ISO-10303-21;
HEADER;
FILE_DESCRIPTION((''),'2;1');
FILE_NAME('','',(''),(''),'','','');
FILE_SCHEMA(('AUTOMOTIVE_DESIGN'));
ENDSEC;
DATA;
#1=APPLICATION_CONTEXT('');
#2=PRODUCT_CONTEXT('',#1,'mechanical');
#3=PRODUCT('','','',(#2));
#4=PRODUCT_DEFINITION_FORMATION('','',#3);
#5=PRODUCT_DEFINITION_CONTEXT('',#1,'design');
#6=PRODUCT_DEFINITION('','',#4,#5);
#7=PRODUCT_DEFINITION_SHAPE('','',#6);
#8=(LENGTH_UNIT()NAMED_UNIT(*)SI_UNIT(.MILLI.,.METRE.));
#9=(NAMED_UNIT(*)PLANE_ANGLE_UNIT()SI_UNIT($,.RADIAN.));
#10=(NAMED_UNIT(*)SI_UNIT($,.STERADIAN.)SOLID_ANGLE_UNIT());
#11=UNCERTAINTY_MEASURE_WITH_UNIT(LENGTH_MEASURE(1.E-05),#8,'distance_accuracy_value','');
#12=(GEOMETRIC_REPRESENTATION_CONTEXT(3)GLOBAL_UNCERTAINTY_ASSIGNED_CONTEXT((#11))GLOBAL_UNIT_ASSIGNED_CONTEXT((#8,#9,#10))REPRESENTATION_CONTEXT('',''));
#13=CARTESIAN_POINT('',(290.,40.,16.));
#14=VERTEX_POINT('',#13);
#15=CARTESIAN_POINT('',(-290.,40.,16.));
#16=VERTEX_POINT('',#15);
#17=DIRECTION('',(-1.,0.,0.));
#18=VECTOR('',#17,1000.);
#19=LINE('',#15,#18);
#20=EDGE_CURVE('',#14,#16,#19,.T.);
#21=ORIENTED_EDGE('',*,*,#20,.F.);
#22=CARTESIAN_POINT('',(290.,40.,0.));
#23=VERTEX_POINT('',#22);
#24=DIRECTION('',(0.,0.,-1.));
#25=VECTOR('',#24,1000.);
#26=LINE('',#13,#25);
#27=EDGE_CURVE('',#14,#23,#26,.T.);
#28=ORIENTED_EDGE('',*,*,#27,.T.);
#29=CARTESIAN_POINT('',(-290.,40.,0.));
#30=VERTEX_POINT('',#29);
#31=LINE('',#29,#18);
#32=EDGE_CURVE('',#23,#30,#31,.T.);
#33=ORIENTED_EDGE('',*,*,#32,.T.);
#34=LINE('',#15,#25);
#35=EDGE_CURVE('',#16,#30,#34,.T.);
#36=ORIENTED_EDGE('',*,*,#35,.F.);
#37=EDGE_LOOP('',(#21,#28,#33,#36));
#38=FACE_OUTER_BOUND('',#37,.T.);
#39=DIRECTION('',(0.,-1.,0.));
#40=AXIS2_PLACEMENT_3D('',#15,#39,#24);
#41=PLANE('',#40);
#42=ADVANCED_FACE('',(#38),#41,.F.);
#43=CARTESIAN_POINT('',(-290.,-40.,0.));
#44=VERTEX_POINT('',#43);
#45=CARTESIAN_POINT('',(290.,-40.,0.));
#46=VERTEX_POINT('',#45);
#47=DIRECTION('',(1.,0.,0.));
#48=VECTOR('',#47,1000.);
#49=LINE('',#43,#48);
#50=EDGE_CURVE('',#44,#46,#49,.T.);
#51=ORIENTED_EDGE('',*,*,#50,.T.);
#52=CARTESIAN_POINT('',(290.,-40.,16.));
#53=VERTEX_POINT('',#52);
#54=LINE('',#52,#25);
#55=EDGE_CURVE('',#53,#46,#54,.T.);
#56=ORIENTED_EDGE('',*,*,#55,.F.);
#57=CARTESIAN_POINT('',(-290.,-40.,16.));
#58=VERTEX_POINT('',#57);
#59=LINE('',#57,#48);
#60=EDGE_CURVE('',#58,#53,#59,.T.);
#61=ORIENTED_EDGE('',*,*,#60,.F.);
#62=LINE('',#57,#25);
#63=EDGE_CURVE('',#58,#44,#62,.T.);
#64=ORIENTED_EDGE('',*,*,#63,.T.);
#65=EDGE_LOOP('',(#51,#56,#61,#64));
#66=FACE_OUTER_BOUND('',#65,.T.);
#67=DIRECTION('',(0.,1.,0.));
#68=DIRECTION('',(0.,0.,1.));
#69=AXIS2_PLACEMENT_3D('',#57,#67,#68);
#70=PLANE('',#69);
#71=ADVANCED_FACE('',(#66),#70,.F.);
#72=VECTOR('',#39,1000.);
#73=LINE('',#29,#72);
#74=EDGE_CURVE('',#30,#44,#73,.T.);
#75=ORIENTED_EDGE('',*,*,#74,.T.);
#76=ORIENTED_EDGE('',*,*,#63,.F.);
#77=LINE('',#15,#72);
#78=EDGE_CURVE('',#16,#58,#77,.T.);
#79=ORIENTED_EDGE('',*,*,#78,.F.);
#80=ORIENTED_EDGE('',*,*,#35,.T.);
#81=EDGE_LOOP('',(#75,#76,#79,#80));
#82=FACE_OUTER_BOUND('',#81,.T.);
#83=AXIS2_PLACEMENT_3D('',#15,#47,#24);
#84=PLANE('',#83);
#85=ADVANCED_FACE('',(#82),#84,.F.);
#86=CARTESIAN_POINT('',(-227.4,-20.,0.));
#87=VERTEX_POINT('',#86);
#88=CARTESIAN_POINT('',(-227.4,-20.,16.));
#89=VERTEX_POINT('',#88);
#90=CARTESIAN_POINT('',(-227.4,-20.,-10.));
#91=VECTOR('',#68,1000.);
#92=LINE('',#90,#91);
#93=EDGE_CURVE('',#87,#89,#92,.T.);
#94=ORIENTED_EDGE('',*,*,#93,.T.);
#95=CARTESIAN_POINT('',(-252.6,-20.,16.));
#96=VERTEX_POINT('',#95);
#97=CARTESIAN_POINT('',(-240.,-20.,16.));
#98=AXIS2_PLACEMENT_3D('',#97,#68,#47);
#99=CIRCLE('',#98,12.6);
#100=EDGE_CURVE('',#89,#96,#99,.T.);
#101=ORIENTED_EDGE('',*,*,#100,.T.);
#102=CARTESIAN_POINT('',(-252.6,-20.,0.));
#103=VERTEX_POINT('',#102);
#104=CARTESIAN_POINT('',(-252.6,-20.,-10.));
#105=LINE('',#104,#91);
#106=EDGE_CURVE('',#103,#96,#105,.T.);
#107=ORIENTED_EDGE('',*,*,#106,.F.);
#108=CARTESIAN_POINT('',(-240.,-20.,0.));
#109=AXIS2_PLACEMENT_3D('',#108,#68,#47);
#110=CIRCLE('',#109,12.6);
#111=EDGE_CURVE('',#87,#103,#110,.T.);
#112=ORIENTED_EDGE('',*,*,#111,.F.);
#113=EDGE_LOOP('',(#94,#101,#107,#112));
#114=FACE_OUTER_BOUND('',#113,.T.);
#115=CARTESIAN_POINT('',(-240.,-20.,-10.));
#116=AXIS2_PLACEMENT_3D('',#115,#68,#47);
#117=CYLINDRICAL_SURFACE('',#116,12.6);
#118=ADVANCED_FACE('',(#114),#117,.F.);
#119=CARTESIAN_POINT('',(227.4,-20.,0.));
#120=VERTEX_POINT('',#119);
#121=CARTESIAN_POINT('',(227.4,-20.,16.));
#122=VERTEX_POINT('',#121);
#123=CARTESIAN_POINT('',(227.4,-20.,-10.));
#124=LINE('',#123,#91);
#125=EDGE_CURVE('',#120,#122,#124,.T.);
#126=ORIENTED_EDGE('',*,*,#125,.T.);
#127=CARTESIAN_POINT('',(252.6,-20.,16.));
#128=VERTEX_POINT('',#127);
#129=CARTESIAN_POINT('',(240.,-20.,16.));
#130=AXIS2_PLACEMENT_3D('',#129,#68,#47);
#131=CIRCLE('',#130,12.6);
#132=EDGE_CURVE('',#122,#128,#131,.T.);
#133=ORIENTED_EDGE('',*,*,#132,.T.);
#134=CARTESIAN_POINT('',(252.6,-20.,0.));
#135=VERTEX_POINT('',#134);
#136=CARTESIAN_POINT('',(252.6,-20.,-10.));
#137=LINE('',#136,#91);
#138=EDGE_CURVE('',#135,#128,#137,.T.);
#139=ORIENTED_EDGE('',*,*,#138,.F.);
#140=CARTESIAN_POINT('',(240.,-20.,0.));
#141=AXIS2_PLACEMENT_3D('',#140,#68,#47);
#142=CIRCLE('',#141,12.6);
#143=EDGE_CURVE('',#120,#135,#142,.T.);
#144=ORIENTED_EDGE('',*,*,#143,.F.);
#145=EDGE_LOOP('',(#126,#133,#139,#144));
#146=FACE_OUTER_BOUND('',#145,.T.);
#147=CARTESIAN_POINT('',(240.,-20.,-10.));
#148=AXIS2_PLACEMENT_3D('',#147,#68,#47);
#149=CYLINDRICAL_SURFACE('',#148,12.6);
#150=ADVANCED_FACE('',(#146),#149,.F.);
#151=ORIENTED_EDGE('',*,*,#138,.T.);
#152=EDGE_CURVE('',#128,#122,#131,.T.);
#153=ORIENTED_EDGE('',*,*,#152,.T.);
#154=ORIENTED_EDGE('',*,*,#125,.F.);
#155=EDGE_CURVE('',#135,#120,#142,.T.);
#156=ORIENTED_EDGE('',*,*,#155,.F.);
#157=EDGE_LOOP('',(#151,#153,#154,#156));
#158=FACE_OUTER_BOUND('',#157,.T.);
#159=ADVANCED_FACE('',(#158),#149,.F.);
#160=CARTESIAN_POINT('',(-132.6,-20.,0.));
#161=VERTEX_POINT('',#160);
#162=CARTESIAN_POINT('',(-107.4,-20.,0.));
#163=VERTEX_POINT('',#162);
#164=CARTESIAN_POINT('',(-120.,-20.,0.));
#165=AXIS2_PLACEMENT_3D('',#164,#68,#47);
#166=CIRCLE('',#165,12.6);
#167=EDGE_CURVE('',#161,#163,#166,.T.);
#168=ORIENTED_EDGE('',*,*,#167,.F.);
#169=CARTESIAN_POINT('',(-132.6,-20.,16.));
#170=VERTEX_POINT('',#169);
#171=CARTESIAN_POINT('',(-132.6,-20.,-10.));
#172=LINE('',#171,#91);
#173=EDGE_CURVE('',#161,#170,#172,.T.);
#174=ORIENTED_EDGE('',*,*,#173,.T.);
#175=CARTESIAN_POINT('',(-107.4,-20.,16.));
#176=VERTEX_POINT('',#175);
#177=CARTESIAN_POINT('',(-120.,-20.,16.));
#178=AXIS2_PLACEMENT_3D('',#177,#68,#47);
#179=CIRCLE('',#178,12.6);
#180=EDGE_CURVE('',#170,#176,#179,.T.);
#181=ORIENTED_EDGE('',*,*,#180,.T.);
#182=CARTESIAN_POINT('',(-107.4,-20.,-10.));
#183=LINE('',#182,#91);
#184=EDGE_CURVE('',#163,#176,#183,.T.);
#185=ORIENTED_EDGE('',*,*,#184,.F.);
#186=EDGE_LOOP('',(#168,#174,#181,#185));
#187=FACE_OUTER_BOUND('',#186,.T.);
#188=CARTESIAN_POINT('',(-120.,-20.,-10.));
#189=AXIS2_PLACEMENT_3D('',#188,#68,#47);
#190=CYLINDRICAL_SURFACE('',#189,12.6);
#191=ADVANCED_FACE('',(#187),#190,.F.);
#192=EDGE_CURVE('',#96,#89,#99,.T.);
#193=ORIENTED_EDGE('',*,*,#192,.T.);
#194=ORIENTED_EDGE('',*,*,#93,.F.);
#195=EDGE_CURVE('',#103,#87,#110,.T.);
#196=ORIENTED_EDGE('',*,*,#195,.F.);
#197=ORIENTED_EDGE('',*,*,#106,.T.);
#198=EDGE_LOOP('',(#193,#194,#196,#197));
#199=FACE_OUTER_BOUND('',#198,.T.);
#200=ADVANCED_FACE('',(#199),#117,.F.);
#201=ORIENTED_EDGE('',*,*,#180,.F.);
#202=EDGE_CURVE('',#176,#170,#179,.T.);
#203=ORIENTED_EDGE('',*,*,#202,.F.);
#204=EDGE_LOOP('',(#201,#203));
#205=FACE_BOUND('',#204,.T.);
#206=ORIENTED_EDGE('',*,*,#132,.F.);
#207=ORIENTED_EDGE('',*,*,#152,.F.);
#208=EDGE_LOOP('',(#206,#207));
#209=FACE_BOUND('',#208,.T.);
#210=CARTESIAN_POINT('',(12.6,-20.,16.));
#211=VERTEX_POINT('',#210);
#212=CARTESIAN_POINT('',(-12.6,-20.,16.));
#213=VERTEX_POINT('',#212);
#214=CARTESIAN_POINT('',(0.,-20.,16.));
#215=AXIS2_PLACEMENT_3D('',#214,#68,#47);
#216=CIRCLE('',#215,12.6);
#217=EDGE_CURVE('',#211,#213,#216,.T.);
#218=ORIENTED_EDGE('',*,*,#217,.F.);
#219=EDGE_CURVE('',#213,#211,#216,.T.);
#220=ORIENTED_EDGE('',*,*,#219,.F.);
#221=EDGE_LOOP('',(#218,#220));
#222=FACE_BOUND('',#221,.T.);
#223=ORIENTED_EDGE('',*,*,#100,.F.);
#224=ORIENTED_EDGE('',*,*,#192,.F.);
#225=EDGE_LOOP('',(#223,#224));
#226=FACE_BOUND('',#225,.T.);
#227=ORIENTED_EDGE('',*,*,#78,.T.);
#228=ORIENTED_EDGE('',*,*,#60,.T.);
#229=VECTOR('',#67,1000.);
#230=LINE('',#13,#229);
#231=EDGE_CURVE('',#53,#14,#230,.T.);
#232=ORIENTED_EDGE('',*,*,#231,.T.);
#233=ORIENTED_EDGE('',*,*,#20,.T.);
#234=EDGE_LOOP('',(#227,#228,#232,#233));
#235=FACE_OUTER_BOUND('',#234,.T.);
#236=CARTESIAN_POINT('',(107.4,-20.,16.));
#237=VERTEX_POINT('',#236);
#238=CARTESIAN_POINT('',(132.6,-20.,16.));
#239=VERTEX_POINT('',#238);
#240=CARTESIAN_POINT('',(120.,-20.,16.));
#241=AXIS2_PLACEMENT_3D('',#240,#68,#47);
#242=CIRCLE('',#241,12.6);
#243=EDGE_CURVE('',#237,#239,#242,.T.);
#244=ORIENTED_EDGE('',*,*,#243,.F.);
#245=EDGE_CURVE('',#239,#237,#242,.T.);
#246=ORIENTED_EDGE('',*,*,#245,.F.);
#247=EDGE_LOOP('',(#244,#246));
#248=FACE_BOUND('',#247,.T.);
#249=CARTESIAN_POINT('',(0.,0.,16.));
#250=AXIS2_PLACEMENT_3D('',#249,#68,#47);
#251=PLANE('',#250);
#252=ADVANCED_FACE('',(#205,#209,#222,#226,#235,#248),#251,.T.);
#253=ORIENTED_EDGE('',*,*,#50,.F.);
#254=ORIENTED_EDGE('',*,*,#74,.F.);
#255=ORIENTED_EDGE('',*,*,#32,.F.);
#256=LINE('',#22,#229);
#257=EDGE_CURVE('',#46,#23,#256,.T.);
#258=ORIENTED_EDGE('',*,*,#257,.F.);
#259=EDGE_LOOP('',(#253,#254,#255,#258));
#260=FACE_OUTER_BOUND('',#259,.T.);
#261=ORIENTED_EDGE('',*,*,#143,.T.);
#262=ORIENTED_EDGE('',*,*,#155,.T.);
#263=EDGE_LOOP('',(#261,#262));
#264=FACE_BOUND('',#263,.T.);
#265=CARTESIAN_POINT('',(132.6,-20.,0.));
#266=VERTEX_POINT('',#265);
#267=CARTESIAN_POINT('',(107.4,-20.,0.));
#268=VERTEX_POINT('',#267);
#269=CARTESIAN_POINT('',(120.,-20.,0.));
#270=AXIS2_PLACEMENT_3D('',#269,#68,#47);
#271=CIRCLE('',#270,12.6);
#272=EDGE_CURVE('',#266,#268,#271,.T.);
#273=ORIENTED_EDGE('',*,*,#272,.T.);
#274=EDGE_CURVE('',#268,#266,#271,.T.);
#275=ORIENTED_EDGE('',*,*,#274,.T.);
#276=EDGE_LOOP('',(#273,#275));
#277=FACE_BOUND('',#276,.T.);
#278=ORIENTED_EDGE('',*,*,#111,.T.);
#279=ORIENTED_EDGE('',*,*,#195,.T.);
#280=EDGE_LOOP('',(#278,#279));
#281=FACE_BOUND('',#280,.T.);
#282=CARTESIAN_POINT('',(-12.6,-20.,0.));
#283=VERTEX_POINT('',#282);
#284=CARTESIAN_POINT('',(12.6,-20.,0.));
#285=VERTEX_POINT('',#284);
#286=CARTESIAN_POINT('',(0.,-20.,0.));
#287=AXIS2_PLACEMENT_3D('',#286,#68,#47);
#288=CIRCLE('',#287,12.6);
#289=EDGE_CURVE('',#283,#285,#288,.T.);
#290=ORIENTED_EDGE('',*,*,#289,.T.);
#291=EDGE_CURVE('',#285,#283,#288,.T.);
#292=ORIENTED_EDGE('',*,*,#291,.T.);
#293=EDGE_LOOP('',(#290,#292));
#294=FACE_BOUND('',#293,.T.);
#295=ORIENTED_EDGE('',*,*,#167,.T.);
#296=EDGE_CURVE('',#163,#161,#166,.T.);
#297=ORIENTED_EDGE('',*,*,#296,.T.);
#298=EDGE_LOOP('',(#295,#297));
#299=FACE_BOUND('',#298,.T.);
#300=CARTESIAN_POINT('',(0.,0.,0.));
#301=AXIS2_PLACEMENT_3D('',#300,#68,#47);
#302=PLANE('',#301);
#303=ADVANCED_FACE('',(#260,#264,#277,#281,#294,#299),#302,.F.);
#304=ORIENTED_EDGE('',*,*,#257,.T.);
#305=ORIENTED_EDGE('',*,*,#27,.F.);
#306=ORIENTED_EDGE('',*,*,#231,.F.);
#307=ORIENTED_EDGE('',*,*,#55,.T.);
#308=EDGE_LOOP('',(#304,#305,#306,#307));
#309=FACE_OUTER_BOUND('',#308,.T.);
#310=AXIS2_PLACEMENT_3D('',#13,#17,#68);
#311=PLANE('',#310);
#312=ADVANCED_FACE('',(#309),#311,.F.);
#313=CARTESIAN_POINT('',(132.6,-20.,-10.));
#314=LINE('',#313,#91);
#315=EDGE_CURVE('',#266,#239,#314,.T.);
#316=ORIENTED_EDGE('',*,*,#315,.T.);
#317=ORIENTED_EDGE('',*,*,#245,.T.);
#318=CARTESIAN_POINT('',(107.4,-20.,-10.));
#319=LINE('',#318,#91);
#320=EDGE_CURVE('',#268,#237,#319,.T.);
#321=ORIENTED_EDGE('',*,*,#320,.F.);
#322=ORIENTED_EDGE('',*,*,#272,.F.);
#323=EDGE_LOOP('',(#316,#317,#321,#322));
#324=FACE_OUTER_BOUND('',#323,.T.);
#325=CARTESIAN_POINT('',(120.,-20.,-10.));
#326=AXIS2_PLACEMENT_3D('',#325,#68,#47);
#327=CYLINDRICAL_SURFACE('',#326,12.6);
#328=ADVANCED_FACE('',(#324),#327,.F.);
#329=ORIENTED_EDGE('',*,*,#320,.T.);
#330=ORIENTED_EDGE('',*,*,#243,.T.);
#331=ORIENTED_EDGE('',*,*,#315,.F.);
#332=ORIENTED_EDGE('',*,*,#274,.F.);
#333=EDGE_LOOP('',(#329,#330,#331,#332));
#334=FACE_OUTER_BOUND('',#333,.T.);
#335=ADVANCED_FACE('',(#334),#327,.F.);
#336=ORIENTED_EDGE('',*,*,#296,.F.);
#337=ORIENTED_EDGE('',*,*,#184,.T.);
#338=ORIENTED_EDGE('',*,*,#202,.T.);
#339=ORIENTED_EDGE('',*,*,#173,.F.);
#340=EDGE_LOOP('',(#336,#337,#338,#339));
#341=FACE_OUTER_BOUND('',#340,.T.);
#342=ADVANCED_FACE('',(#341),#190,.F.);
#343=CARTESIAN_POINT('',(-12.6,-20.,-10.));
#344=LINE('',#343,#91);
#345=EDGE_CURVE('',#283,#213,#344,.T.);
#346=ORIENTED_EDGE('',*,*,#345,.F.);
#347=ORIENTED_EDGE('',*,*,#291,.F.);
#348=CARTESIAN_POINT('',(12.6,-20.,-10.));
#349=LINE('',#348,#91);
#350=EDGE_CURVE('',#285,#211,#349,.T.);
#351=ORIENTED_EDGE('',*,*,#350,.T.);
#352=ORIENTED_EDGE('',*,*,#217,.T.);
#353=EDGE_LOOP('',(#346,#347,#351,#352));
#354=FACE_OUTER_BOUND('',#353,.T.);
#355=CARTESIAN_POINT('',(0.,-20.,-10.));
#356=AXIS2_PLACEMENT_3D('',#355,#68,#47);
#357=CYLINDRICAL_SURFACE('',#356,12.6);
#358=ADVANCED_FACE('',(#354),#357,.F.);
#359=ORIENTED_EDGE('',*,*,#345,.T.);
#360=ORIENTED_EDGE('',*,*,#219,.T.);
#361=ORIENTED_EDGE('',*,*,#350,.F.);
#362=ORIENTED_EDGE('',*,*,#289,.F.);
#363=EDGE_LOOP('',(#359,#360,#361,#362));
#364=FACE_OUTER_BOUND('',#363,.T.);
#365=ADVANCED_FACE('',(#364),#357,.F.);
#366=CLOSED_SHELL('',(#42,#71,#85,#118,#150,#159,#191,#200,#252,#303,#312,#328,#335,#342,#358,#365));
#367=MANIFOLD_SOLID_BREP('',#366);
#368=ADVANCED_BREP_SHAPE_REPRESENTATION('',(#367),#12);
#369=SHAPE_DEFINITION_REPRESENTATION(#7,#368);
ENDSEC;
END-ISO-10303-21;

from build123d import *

# Parameters (mm, degrees)
BAR_PROFILE_SKETCH_W             = 580
BAR_PROFILE_SKETCH_H             = 80
FLAT_BAR_580X80X16_DEPTH         = 16
HOLE_ROW_SKETCH_R                = 12.6
THROUGH_HOLES_5X_PITCH_120_DEPTH = 26


with BuildPart() as part:
    # Bar Profile Sketch → Flat Bar 580x80x16 (new body)
    with BuildSketch(Plane.XY):
        Rectangle(BAR_PROFILE_SKETCH_W, BAR_PROFILE_SKETCH_H)
    extrude(amount=FLAT_BAR_580X80X16_DEPTH)

    # Hole Row Sketch → Through Holes 5x Pitch 120 (cut)
    with BuildSketch(Plane.XY.offset(16)):
        with Locations((-240, -20)):
            Circle(HOLE_ROW_SKETCH_R)
        with Locations((-120, -20)):
            Circle(HOLE_ROW_SKETCH_R)
        with Locations((0, -20)):
            Circle(HOLE_ROW_SKETCH_R)
        with Locations((120, -20)):
            Circle(HOLE_ROW_SKETCH_R)
        with Locations((240, -20)):
            Circle(HOLE_ROW_SKETCH_R)
    extrude(amount=-THROUGH_HOLES_5X_PITCH_120_DEPTH, mode=Mode.SUBTRACT)


solid = part.part
